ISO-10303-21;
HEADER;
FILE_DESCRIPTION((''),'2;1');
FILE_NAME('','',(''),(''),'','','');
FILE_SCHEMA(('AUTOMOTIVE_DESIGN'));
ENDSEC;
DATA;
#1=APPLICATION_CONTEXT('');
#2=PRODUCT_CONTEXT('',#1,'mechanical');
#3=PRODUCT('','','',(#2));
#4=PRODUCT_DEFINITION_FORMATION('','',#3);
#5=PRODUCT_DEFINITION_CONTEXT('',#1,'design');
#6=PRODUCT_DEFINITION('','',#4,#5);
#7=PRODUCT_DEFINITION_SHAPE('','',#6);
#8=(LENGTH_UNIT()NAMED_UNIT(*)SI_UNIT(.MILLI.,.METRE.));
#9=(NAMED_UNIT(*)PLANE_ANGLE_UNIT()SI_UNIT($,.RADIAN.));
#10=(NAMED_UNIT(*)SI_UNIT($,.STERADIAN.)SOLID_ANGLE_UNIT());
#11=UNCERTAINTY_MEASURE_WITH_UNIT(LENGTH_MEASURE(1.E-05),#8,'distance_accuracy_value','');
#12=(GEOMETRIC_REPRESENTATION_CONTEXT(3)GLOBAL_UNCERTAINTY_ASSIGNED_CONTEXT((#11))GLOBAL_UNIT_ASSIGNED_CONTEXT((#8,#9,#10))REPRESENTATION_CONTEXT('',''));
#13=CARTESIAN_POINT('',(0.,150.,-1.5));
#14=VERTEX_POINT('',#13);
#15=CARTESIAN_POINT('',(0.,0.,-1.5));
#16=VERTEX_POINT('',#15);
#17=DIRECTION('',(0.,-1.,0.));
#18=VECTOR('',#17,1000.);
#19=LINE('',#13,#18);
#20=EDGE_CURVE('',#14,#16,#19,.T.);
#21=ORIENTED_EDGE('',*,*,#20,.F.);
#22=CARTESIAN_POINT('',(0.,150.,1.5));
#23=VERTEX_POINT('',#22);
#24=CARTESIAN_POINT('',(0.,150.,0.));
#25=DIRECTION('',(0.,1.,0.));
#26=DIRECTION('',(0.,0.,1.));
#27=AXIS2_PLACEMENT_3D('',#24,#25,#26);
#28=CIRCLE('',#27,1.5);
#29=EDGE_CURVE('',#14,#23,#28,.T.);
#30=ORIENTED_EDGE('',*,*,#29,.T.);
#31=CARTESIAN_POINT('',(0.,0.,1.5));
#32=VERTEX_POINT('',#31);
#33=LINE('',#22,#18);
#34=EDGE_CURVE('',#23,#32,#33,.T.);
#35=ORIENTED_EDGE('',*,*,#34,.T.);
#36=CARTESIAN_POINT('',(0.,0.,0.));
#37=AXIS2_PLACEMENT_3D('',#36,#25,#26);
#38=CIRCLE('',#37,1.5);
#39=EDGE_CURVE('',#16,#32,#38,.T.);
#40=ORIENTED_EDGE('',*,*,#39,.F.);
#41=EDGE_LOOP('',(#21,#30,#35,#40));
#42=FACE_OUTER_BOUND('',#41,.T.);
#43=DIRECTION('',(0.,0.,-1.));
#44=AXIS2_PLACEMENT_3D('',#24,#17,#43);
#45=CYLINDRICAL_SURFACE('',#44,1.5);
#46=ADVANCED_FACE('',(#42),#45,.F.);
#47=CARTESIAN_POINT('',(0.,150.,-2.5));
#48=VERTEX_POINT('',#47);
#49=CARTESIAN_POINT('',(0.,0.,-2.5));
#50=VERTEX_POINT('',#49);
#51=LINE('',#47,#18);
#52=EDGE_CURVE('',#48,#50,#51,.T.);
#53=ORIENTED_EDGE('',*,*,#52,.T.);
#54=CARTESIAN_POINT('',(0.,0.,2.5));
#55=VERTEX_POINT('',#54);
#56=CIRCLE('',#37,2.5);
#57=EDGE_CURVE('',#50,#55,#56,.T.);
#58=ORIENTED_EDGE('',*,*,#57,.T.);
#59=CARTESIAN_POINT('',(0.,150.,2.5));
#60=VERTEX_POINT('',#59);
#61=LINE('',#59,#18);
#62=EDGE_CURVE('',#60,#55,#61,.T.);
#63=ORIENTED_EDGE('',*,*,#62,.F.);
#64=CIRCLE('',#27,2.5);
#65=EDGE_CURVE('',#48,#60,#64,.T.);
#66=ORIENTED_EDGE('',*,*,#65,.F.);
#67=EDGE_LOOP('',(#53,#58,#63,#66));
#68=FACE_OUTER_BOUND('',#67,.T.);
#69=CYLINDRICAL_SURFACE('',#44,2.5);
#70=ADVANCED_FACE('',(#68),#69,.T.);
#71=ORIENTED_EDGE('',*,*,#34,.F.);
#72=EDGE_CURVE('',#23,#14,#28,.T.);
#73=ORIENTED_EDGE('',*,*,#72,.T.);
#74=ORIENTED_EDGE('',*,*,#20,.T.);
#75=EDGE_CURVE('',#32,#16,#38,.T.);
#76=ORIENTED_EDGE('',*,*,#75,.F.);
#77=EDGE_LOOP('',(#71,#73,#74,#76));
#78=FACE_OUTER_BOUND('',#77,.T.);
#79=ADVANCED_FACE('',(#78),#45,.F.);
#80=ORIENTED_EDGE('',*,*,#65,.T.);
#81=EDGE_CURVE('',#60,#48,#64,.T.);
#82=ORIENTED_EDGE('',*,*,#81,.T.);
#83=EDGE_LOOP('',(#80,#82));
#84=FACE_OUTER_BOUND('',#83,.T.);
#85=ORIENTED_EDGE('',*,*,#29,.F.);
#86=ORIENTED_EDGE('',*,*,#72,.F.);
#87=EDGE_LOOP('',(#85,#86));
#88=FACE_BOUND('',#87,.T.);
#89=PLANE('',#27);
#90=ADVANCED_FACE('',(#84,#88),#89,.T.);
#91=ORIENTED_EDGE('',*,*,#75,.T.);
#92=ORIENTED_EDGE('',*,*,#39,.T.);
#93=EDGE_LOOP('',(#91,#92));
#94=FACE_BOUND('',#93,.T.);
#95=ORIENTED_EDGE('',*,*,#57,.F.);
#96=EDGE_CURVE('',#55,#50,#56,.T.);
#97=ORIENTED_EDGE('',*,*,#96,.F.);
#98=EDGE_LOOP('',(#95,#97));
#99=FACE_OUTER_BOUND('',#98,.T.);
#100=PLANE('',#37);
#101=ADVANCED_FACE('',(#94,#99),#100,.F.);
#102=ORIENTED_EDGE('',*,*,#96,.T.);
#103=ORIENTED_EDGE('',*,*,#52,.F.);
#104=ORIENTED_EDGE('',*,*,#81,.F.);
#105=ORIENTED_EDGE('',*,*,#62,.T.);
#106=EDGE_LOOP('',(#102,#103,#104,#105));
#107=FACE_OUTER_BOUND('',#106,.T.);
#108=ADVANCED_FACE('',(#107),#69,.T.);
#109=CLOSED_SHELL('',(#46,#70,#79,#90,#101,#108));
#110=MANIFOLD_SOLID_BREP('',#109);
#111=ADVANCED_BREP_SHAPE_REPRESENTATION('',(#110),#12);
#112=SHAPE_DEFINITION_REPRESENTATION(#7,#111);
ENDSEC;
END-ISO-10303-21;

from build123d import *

# Parameters (mm, degrees)
SKETCH_1_R      = 2.5
SKETCH_1_R_2    = 1.5
EXTRUDE_1_DEPTH = 150


with BuildPart() as part:
    # 草图1 → 凸台-拉伸1 (new body)
    with BuildSketch(Plane(origin=(0, 0, 0), x_dir=(1, 0, 0), z_dir=(0, 1, 0))):
        with Locations(Location((0, 0, 0), (0, 0, 270))):
            Circle(SKETCH_1_R)
        with Locations(Location((0, 0, 0), (0, 0, 270))):
            Circle(SKETCH_1_R_2, mode=Mode.SUBTRACT)
    extrude(amount=EXTRUDE_1_DEPTH)


solid = part.part
